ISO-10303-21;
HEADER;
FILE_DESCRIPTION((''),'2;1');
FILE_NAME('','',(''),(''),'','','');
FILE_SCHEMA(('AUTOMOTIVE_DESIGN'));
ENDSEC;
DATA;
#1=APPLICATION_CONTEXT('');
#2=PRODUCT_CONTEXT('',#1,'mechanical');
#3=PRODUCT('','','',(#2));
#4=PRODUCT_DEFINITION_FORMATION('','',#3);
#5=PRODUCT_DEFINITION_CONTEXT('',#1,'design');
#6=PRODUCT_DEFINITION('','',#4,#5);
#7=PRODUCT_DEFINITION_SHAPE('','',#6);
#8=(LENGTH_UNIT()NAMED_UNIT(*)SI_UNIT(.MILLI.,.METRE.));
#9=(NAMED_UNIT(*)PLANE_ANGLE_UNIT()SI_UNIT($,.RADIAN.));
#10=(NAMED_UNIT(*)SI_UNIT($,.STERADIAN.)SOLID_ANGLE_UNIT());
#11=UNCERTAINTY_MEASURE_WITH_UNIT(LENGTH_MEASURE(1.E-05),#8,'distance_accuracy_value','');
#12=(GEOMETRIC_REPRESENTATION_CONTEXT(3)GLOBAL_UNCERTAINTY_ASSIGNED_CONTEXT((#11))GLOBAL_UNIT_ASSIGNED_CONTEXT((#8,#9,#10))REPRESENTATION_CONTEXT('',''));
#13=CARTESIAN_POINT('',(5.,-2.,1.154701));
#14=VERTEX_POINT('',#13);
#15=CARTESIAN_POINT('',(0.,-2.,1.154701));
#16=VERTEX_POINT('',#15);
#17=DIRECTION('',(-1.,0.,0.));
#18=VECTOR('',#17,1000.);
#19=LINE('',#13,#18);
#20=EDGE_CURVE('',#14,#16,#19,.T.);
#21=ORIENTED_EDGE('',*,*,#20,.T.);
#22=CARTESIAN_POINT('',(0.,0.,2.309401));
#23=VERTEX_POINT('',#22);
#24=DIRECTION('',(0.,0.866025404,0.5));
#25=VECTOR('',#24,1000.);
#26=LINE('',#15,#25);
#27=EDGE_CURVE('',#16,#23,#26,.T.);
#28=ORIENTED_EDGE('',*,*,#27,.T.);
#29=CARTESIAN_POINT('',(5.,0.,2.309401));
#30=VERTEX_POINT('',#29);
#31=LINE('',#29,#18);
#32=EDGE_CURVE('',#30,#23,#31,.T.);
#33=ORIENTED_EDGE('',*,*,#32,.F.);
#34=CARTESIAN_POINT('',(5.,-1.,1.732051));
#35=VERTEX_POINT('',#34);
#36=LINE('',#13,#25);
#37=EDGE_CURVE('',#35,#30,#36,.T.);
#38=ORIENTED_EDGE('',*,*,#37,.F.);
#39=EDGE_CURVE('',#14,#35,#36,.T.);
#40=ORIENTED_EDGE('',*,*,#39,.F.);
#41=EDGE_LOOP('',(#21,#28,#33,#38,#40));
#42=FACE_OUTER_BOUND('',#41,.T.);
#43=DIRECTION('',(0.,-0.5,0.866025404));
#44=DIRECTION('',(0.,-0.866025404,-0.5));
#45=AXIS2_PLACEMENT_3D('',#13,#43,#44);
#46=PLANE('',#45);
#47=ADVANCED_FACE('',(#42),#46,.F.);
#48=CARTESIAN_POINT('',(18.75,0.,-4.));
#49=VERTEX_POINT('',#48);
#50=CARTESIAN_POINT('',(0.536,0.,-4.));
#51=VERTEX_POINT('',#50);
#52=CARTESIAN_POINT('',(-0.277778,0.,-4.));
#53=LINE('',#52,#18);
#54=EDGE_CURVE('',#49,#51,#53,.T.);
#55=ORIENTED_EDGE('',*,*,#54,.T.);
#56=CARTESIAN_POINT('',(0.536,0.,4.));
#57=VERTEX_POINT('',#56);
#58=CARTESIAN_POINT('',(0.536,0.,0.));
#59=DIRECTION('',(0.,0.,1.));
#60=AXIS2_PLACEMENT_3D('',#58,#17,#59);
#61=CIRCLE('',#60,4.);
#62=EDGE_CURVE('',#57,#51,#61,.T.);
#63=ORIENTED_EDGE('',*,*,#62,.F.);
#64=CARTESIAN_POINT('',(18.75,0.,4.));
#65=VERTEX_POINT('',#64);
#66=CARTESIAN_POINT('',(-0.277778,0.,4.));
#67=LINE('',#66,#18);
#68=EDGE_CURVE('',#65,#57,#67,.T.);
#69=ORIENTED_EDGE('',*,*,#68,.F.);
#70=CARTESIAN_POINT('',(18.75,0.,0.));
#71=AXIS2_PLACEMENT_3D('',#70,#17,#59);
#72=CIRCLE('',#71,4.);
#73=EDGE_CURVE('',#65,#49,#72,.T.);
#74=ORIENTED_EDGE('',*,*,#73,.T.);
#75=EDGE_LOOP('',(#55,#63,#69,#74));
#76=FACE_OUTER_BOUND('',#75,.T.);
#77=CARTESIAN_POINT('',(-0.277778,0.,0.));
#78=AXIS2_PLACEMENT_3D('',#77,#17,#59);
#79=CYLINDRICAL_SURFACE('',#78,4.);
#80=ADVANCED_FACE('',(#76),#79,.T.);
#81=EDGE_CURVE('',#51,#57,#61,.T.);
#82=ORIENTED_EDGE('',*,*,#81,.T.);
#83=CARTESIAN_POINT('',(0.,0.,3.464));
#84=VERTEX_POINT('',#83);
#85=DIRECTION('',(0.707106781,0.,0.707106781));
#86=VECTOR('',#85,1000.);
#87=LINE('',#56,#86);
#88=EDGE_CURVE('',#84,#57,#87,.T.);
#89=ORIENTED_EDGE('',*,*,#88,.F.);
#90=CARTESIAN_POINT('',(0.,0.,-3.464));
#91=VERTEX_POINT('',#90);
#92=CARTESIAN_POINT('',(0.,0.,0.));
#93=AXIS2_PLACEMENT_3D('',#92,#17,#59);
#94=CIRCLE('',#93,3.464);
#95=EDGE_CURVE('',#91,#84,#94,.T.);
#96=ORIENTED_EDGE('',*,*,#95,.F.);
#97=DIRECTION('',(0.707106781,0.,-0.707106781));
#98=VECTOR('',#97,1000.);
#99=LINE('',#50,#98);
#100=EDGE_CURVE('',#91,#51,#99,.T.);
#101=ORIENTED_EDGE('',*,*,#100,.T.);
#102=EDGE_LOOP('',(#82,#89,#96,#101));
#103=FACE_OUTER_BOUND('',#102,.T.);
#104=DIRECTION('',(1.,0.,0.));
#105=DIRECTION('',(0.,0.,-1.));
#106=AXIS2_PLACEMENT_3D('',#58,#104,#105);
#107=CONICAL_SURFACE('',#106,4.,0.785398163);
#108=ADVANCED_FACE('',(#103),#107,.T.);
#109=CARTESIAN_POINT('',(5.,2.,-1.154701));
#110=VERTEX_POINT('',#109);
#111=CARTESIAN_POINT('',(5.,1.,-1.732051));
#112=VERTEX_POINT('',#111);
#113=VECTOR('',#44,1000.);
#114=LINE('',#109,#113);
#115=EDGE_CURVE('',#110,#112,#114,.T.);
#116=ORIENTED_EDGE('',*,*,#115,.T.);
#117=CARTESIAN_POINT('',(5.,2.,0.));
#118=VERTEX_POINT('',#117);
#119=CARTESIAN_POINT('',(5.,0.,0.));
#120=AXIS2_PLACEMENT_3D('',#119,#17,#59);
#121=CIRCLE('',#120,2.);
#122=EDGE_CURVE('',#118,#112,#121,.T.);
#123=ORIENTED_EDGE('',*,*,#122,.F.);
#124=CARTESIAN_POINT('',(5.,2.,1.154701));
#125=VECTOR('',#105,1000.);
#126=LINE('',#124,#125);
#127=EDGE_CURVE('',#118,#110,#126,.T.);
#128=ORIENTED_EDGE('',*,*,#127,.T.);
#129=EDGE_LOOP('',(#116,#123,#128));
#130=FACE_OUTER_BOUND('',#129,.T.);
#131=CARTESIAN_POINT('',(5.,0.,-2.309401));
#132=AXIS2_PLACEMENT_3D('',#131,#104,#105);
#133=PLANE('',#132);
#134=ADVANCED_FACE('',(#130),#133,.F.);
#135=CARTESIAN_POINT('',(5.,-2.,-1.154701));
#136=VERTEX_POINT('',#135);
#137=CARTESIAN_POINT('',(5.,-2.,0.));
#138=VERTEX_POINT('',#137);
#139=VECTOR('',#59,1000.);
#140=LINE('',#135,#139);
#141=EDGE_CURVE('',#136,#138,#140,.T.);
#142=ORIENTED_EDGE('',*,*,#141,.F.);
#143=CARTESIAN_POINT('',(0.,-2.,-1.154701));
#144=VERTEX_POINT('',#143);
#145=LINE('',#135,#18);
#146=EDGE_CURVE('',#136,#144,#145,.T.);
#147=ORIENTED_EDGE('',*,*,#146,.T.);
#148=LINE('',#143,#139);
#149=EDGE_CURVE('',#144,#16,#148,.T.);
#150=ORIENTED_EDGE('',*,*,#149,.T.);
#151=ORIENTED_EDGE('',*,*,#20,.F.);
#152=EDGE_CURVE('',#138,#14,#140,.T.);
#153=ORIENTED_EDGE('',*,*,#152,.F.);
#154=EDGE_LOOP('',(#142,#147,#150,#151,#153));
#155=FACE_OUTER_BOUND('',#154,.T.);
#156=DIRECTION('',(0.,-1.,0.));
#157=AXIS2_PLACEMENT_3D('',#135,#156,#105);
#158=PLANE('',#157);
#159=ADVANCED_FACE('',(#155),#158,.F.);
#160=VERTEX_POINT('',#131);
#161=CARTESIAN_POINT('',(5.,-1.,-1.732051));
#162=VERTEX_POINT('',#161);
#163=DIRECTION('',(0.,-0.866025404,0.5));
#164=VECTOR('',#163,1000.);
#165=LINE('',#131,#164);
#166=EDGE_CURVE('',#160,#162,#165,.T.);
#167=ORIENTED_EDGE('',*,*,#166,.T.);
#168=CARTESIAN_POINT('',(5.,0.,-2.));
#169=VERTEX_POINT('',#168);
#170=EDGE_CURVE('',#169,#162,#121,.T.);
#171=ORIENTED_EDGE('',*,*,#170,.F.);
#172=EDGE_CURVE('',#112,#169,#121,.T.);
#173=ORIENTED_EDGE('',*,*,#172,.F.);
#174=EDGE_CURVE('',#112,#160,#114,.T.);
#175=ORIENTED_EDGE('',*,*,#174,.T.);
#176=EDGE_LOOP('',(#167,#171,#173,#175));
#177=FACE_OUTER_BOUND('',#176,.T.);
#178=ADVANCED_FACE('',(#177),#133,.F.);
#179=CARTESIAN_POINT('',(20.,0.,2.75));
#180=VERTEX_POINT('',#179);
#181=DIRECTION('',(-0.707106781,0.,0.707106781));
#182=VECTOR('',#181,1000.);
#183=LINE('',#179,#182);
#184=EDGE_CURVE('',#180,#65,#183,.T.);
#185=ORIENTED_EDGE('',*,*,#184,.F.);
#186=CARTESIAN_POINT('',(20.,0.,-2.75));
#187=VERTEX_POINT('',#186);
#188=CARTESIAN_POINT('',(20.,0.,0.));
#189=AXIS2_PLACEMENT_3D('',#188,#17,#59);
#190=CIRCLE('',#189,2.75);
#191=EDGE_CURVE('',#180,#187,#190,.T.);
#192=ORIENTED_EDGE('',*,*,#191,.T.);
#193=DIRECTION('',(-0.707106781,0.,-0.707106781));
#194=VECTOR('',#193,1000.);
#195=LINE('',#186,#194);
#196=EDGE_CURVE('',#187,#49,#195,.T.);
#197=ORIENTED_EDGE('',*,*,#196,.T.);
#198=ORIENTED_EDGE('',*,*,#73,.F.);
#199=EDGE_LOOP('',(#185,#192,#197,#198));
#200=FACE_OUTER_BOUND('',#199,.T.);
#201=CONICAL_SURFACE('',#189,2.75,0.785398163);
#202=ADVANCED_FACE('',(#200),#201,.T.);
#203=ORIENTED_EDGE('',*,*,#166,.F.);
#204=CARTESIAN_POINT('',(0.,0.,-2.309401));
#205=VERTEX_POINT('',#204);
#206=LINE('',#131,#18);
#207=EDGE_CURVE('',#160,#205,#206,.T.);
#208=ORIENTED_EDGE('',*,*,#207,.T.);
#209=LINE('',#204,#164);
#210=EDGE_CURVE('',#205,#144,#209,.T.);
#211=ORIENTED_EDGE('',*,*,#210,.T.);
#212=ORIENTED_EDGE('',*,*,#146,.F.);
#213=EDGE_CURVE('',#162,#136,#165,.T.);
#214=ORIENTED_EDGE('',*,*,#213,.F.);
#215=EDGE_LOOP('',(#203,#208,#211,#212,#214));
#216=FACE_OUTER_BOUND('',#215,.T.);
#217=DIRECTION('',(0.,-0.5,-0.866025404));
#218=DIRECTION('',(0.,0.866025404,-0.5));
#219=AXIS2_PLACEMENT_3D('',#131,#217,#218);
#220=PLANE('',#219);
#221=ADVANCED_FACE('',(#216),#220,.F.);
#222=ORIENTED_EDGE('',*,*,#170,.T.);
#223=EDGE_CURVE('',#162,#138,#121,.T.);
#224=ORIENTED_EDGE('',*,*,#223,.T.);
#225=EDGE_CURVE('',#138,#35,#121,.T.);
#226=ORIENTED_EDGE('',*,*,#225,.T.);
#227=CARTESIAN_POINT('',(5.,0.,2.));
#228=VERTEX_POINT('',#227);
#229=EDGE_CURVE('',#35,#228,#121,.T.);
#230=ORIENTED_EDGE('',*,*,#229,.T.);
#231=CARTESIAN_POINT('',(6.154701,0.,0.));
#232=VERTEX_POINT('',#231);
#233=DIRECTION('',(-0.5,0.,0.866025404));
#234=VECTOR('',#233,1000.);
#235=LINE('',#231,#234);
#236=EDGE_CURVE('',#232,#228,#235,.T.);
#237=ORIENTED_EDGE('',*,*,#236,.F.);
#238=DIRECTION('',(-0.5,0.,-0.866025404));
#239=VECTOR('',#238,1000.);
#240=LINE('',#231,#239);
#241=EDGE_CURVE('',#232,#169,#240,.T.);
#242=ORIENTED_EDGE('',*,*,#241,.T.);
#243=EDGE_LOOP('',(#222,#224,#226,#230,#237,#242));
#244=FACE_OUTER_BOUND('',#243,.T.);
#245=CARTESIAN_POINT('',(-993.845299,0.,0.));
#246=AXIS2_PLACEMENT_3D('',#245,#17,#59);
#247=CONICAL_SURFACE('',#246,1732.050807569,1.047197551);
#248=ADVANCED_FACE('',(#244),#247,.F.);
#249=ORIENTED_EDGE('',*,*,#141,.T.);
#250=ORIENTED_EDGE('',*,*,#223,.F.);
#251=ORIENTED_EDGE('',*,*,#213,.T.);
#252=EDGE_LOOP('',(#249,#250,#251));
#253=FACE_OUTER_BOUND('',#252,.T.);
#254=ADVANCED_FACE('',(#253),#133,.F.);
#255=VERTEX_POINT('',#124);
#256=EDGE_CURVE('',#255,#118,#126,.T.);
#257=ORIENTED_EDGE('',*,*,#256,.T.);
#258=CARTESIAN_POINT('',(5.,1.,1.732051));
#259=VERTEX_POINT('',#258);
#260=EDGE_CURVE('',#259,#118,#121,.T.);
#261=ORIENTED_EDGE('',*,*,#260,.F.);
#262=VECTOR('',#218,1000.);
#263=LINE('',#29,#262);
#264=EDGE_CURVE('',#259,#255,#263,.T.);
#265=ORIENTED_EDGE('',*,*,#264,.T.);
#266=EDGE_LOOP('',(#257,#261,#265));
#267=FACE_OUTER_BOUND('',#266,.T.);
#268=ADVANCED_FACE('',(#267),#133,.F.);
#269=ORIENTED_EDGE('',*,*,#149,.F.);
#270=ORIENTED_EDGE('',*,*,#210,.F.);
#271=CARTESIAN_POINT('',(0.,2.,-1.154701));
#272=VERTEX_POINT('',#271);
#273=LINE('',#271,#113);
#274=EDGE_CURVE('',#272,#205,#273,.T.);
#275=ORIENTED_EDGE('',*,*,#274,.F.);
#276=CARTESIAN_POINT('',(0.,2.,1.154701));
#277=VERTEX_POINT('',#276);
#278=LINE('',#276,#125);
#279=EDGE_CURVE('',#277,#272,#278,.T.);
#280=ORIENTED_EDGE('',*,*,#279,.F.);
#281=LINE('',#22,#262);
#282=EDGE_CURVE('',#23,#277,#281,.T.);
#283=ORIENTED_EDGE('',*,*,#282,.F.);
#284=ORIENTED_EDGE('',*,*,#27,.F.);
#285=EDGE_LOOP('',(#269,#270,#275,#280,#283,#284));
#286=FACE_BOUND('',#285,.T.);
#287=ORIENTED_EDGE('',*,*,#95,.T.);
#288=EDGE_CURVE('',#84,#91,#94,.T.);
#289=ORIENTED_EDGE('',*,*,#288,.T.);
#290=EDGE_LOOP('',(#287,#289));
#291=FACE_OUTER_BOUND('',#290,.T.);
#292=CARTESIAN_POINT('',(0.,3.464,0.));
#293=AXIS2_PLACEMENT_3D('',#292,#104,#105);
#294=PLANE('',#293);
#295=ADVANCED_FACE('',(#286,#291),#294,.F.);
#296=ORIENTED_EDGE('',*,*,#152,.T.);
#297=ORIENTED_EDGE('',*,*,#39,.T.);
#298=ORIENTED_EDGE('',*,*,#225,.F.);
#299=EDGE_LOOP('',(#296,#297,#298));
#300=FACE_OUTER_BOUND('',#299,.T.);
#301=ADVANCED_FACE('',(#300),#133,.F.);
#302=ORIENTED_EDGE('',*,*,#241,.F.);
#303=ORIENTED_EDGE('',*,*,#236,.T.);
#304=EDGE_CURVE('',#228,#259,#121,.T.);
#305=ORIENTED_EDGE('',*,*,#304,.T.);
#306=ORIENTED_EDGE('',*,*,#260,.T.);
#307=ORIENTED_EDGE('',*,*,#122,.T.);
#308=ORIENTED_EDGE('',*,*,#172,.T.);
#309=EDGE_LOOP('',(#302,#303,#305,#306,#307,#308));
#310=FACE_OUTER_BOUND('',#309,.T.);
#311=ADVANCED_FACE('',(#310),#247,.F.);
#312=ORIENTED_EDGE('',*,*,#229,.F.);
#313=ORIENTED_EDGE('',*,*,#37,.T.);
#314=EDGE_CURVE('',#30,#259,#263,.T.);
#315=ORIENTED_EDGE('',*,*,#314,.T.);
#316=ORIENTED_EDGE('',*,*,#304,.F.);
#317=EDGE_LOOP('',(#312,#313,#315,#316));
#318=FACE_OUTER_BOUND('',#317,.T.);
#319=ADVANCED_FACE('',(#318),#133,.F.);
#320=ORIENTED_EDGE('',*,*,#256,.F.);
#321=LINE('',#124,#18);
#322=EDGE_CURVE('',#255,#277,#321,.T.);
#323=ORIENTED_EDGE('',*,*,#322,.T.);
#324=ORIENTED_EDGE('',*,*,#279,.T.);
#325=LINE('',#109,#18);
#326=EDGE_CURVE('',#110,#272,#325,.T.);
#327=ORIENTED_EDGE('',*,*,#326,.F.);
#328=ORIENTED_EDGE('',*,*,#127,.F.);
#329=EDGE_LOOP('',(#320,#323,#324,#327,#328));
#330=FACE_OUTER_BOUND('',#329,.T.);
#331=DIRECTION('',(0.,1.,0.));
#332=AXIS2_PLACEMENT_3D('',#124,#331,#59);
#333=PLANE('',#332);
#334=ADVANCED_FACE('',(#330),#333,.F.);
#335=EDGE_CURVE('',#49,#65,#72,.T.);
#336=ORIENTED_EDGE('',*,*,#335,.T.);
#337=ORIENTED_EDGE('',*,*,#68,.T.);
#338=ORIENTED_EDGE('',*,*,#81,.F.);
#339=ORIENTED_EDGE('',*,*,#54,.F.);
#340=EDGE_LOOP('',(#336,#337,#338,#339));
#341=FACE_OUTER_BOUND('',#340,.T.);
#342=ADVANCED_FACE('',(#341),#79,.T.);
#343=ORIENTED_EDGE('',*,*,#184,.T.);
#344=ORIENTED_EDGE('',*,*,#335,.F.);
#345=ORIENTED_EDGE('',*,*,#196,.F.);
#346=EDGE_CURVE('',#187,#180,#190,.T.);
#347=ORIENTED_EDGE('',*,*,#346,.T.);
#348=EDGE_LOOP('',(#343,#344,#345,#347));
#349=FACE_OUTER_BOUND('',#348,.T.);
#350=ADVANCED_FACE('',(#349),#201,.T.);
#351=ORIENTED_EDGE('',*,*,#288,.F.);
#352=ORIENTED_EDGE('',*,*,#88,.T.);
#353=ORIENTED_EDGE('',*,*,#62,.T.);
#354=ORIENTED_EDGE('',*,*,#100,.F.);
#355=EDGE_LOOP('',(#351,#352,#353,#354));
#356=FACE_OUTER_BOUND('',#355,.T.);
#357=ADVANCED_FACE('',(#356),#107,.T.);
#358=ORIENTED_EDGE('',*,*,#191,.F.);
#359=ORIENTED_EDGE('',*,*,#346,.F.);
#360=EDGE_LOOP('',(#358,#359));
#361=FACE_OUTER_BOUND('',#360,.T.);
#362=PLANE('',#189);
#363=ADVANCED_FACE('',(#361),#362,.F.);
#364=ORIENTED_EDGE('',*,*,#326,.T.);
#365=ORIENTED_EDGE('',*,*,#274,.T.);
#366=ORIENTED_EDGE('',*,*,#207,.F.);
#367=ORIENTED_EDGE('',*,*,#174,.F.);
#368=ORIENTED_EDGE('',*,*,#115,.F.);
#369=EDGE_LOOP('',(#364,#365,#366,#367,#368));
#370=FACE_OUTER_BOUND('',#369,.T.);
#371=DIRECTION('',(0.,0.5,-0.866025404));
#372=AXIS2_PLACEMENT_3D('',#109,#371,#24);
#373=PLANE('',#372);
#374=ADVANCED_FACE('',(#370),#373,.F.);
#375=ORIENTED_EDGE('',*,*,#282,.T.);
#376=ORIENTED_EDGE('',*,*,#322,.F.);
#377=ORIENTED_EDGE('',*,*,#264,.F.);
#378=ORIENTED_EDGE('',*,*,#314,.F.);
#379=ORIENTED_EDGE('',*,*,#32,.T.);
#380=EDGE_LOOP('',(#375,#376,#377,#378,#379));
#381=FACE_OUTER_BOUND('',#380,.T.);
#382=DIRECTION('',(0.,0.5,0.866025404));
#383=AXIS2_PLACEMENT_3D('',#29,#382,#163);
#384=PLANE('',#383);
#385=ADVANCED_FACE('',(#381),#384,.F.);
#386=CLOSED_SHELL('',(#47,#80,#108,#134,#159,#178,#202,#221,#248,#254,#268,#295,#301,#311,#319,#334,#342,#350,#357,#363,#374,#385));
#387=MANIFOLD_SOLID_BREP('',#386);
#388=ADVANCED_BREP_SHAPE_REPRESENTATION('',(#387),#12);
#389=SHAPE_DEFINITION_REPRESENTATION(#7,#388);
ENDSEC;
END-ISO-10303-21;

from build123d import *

# Parameters (mm, degrees)
CUT_EXTRUDE_1_DEPTH = 5


with BuildPart() as part:
    # 草图1 → Revolve 587 (revolve)
    with BuildSketch(Plane.XY, mode=Mode.PRIVATE) as revolve_587_sk:
        Polygon((0, 0), (20, 0), (20, 2.75), (18.75, 4), (0.536, 4), (0, 3.464), align=None)
    revolve(revolve_587_sk.sketch.rotate(Axis((-0.277777778, 0, 0), (1, 0, 0)), 90), axis=Axis((-0.277777778, 0, 0), (1, 0, 0)))

    # 草图2 → 切除-拉伸1 (cut)
    with BuildSketch(Plane.ZY):
        Polygon((-1.154700538, -2), (1.154700538, -2), (2.309401077, 0), (1.154700538, 2), (-1.154700538, 2), (-2.309401077, 0), align=None)
    extrude(amount=-CUT_EXTRUDE_1_DEPTH, mode=Mode.SUBTRACT)

    # 草图4 → 切除-旋转2 (revolve, cut)
    with BuildSketch(Plane.XY, mode=Mode.PRIVATE) as cut_revolve_2_sk:
        Polygon((5, 2), (6.154700538, 0), (5, 0), align=None)
    revolve(cut_revolve_2_sk.sketch.rotate(Axis((-0.277777778, 0, 0), (1, 0, 0)), 90), axis=Axis((-0.277777778, 0, 0), (1, 0, 0)), mode=Mode.SUBTRACT)


solid = part.part
